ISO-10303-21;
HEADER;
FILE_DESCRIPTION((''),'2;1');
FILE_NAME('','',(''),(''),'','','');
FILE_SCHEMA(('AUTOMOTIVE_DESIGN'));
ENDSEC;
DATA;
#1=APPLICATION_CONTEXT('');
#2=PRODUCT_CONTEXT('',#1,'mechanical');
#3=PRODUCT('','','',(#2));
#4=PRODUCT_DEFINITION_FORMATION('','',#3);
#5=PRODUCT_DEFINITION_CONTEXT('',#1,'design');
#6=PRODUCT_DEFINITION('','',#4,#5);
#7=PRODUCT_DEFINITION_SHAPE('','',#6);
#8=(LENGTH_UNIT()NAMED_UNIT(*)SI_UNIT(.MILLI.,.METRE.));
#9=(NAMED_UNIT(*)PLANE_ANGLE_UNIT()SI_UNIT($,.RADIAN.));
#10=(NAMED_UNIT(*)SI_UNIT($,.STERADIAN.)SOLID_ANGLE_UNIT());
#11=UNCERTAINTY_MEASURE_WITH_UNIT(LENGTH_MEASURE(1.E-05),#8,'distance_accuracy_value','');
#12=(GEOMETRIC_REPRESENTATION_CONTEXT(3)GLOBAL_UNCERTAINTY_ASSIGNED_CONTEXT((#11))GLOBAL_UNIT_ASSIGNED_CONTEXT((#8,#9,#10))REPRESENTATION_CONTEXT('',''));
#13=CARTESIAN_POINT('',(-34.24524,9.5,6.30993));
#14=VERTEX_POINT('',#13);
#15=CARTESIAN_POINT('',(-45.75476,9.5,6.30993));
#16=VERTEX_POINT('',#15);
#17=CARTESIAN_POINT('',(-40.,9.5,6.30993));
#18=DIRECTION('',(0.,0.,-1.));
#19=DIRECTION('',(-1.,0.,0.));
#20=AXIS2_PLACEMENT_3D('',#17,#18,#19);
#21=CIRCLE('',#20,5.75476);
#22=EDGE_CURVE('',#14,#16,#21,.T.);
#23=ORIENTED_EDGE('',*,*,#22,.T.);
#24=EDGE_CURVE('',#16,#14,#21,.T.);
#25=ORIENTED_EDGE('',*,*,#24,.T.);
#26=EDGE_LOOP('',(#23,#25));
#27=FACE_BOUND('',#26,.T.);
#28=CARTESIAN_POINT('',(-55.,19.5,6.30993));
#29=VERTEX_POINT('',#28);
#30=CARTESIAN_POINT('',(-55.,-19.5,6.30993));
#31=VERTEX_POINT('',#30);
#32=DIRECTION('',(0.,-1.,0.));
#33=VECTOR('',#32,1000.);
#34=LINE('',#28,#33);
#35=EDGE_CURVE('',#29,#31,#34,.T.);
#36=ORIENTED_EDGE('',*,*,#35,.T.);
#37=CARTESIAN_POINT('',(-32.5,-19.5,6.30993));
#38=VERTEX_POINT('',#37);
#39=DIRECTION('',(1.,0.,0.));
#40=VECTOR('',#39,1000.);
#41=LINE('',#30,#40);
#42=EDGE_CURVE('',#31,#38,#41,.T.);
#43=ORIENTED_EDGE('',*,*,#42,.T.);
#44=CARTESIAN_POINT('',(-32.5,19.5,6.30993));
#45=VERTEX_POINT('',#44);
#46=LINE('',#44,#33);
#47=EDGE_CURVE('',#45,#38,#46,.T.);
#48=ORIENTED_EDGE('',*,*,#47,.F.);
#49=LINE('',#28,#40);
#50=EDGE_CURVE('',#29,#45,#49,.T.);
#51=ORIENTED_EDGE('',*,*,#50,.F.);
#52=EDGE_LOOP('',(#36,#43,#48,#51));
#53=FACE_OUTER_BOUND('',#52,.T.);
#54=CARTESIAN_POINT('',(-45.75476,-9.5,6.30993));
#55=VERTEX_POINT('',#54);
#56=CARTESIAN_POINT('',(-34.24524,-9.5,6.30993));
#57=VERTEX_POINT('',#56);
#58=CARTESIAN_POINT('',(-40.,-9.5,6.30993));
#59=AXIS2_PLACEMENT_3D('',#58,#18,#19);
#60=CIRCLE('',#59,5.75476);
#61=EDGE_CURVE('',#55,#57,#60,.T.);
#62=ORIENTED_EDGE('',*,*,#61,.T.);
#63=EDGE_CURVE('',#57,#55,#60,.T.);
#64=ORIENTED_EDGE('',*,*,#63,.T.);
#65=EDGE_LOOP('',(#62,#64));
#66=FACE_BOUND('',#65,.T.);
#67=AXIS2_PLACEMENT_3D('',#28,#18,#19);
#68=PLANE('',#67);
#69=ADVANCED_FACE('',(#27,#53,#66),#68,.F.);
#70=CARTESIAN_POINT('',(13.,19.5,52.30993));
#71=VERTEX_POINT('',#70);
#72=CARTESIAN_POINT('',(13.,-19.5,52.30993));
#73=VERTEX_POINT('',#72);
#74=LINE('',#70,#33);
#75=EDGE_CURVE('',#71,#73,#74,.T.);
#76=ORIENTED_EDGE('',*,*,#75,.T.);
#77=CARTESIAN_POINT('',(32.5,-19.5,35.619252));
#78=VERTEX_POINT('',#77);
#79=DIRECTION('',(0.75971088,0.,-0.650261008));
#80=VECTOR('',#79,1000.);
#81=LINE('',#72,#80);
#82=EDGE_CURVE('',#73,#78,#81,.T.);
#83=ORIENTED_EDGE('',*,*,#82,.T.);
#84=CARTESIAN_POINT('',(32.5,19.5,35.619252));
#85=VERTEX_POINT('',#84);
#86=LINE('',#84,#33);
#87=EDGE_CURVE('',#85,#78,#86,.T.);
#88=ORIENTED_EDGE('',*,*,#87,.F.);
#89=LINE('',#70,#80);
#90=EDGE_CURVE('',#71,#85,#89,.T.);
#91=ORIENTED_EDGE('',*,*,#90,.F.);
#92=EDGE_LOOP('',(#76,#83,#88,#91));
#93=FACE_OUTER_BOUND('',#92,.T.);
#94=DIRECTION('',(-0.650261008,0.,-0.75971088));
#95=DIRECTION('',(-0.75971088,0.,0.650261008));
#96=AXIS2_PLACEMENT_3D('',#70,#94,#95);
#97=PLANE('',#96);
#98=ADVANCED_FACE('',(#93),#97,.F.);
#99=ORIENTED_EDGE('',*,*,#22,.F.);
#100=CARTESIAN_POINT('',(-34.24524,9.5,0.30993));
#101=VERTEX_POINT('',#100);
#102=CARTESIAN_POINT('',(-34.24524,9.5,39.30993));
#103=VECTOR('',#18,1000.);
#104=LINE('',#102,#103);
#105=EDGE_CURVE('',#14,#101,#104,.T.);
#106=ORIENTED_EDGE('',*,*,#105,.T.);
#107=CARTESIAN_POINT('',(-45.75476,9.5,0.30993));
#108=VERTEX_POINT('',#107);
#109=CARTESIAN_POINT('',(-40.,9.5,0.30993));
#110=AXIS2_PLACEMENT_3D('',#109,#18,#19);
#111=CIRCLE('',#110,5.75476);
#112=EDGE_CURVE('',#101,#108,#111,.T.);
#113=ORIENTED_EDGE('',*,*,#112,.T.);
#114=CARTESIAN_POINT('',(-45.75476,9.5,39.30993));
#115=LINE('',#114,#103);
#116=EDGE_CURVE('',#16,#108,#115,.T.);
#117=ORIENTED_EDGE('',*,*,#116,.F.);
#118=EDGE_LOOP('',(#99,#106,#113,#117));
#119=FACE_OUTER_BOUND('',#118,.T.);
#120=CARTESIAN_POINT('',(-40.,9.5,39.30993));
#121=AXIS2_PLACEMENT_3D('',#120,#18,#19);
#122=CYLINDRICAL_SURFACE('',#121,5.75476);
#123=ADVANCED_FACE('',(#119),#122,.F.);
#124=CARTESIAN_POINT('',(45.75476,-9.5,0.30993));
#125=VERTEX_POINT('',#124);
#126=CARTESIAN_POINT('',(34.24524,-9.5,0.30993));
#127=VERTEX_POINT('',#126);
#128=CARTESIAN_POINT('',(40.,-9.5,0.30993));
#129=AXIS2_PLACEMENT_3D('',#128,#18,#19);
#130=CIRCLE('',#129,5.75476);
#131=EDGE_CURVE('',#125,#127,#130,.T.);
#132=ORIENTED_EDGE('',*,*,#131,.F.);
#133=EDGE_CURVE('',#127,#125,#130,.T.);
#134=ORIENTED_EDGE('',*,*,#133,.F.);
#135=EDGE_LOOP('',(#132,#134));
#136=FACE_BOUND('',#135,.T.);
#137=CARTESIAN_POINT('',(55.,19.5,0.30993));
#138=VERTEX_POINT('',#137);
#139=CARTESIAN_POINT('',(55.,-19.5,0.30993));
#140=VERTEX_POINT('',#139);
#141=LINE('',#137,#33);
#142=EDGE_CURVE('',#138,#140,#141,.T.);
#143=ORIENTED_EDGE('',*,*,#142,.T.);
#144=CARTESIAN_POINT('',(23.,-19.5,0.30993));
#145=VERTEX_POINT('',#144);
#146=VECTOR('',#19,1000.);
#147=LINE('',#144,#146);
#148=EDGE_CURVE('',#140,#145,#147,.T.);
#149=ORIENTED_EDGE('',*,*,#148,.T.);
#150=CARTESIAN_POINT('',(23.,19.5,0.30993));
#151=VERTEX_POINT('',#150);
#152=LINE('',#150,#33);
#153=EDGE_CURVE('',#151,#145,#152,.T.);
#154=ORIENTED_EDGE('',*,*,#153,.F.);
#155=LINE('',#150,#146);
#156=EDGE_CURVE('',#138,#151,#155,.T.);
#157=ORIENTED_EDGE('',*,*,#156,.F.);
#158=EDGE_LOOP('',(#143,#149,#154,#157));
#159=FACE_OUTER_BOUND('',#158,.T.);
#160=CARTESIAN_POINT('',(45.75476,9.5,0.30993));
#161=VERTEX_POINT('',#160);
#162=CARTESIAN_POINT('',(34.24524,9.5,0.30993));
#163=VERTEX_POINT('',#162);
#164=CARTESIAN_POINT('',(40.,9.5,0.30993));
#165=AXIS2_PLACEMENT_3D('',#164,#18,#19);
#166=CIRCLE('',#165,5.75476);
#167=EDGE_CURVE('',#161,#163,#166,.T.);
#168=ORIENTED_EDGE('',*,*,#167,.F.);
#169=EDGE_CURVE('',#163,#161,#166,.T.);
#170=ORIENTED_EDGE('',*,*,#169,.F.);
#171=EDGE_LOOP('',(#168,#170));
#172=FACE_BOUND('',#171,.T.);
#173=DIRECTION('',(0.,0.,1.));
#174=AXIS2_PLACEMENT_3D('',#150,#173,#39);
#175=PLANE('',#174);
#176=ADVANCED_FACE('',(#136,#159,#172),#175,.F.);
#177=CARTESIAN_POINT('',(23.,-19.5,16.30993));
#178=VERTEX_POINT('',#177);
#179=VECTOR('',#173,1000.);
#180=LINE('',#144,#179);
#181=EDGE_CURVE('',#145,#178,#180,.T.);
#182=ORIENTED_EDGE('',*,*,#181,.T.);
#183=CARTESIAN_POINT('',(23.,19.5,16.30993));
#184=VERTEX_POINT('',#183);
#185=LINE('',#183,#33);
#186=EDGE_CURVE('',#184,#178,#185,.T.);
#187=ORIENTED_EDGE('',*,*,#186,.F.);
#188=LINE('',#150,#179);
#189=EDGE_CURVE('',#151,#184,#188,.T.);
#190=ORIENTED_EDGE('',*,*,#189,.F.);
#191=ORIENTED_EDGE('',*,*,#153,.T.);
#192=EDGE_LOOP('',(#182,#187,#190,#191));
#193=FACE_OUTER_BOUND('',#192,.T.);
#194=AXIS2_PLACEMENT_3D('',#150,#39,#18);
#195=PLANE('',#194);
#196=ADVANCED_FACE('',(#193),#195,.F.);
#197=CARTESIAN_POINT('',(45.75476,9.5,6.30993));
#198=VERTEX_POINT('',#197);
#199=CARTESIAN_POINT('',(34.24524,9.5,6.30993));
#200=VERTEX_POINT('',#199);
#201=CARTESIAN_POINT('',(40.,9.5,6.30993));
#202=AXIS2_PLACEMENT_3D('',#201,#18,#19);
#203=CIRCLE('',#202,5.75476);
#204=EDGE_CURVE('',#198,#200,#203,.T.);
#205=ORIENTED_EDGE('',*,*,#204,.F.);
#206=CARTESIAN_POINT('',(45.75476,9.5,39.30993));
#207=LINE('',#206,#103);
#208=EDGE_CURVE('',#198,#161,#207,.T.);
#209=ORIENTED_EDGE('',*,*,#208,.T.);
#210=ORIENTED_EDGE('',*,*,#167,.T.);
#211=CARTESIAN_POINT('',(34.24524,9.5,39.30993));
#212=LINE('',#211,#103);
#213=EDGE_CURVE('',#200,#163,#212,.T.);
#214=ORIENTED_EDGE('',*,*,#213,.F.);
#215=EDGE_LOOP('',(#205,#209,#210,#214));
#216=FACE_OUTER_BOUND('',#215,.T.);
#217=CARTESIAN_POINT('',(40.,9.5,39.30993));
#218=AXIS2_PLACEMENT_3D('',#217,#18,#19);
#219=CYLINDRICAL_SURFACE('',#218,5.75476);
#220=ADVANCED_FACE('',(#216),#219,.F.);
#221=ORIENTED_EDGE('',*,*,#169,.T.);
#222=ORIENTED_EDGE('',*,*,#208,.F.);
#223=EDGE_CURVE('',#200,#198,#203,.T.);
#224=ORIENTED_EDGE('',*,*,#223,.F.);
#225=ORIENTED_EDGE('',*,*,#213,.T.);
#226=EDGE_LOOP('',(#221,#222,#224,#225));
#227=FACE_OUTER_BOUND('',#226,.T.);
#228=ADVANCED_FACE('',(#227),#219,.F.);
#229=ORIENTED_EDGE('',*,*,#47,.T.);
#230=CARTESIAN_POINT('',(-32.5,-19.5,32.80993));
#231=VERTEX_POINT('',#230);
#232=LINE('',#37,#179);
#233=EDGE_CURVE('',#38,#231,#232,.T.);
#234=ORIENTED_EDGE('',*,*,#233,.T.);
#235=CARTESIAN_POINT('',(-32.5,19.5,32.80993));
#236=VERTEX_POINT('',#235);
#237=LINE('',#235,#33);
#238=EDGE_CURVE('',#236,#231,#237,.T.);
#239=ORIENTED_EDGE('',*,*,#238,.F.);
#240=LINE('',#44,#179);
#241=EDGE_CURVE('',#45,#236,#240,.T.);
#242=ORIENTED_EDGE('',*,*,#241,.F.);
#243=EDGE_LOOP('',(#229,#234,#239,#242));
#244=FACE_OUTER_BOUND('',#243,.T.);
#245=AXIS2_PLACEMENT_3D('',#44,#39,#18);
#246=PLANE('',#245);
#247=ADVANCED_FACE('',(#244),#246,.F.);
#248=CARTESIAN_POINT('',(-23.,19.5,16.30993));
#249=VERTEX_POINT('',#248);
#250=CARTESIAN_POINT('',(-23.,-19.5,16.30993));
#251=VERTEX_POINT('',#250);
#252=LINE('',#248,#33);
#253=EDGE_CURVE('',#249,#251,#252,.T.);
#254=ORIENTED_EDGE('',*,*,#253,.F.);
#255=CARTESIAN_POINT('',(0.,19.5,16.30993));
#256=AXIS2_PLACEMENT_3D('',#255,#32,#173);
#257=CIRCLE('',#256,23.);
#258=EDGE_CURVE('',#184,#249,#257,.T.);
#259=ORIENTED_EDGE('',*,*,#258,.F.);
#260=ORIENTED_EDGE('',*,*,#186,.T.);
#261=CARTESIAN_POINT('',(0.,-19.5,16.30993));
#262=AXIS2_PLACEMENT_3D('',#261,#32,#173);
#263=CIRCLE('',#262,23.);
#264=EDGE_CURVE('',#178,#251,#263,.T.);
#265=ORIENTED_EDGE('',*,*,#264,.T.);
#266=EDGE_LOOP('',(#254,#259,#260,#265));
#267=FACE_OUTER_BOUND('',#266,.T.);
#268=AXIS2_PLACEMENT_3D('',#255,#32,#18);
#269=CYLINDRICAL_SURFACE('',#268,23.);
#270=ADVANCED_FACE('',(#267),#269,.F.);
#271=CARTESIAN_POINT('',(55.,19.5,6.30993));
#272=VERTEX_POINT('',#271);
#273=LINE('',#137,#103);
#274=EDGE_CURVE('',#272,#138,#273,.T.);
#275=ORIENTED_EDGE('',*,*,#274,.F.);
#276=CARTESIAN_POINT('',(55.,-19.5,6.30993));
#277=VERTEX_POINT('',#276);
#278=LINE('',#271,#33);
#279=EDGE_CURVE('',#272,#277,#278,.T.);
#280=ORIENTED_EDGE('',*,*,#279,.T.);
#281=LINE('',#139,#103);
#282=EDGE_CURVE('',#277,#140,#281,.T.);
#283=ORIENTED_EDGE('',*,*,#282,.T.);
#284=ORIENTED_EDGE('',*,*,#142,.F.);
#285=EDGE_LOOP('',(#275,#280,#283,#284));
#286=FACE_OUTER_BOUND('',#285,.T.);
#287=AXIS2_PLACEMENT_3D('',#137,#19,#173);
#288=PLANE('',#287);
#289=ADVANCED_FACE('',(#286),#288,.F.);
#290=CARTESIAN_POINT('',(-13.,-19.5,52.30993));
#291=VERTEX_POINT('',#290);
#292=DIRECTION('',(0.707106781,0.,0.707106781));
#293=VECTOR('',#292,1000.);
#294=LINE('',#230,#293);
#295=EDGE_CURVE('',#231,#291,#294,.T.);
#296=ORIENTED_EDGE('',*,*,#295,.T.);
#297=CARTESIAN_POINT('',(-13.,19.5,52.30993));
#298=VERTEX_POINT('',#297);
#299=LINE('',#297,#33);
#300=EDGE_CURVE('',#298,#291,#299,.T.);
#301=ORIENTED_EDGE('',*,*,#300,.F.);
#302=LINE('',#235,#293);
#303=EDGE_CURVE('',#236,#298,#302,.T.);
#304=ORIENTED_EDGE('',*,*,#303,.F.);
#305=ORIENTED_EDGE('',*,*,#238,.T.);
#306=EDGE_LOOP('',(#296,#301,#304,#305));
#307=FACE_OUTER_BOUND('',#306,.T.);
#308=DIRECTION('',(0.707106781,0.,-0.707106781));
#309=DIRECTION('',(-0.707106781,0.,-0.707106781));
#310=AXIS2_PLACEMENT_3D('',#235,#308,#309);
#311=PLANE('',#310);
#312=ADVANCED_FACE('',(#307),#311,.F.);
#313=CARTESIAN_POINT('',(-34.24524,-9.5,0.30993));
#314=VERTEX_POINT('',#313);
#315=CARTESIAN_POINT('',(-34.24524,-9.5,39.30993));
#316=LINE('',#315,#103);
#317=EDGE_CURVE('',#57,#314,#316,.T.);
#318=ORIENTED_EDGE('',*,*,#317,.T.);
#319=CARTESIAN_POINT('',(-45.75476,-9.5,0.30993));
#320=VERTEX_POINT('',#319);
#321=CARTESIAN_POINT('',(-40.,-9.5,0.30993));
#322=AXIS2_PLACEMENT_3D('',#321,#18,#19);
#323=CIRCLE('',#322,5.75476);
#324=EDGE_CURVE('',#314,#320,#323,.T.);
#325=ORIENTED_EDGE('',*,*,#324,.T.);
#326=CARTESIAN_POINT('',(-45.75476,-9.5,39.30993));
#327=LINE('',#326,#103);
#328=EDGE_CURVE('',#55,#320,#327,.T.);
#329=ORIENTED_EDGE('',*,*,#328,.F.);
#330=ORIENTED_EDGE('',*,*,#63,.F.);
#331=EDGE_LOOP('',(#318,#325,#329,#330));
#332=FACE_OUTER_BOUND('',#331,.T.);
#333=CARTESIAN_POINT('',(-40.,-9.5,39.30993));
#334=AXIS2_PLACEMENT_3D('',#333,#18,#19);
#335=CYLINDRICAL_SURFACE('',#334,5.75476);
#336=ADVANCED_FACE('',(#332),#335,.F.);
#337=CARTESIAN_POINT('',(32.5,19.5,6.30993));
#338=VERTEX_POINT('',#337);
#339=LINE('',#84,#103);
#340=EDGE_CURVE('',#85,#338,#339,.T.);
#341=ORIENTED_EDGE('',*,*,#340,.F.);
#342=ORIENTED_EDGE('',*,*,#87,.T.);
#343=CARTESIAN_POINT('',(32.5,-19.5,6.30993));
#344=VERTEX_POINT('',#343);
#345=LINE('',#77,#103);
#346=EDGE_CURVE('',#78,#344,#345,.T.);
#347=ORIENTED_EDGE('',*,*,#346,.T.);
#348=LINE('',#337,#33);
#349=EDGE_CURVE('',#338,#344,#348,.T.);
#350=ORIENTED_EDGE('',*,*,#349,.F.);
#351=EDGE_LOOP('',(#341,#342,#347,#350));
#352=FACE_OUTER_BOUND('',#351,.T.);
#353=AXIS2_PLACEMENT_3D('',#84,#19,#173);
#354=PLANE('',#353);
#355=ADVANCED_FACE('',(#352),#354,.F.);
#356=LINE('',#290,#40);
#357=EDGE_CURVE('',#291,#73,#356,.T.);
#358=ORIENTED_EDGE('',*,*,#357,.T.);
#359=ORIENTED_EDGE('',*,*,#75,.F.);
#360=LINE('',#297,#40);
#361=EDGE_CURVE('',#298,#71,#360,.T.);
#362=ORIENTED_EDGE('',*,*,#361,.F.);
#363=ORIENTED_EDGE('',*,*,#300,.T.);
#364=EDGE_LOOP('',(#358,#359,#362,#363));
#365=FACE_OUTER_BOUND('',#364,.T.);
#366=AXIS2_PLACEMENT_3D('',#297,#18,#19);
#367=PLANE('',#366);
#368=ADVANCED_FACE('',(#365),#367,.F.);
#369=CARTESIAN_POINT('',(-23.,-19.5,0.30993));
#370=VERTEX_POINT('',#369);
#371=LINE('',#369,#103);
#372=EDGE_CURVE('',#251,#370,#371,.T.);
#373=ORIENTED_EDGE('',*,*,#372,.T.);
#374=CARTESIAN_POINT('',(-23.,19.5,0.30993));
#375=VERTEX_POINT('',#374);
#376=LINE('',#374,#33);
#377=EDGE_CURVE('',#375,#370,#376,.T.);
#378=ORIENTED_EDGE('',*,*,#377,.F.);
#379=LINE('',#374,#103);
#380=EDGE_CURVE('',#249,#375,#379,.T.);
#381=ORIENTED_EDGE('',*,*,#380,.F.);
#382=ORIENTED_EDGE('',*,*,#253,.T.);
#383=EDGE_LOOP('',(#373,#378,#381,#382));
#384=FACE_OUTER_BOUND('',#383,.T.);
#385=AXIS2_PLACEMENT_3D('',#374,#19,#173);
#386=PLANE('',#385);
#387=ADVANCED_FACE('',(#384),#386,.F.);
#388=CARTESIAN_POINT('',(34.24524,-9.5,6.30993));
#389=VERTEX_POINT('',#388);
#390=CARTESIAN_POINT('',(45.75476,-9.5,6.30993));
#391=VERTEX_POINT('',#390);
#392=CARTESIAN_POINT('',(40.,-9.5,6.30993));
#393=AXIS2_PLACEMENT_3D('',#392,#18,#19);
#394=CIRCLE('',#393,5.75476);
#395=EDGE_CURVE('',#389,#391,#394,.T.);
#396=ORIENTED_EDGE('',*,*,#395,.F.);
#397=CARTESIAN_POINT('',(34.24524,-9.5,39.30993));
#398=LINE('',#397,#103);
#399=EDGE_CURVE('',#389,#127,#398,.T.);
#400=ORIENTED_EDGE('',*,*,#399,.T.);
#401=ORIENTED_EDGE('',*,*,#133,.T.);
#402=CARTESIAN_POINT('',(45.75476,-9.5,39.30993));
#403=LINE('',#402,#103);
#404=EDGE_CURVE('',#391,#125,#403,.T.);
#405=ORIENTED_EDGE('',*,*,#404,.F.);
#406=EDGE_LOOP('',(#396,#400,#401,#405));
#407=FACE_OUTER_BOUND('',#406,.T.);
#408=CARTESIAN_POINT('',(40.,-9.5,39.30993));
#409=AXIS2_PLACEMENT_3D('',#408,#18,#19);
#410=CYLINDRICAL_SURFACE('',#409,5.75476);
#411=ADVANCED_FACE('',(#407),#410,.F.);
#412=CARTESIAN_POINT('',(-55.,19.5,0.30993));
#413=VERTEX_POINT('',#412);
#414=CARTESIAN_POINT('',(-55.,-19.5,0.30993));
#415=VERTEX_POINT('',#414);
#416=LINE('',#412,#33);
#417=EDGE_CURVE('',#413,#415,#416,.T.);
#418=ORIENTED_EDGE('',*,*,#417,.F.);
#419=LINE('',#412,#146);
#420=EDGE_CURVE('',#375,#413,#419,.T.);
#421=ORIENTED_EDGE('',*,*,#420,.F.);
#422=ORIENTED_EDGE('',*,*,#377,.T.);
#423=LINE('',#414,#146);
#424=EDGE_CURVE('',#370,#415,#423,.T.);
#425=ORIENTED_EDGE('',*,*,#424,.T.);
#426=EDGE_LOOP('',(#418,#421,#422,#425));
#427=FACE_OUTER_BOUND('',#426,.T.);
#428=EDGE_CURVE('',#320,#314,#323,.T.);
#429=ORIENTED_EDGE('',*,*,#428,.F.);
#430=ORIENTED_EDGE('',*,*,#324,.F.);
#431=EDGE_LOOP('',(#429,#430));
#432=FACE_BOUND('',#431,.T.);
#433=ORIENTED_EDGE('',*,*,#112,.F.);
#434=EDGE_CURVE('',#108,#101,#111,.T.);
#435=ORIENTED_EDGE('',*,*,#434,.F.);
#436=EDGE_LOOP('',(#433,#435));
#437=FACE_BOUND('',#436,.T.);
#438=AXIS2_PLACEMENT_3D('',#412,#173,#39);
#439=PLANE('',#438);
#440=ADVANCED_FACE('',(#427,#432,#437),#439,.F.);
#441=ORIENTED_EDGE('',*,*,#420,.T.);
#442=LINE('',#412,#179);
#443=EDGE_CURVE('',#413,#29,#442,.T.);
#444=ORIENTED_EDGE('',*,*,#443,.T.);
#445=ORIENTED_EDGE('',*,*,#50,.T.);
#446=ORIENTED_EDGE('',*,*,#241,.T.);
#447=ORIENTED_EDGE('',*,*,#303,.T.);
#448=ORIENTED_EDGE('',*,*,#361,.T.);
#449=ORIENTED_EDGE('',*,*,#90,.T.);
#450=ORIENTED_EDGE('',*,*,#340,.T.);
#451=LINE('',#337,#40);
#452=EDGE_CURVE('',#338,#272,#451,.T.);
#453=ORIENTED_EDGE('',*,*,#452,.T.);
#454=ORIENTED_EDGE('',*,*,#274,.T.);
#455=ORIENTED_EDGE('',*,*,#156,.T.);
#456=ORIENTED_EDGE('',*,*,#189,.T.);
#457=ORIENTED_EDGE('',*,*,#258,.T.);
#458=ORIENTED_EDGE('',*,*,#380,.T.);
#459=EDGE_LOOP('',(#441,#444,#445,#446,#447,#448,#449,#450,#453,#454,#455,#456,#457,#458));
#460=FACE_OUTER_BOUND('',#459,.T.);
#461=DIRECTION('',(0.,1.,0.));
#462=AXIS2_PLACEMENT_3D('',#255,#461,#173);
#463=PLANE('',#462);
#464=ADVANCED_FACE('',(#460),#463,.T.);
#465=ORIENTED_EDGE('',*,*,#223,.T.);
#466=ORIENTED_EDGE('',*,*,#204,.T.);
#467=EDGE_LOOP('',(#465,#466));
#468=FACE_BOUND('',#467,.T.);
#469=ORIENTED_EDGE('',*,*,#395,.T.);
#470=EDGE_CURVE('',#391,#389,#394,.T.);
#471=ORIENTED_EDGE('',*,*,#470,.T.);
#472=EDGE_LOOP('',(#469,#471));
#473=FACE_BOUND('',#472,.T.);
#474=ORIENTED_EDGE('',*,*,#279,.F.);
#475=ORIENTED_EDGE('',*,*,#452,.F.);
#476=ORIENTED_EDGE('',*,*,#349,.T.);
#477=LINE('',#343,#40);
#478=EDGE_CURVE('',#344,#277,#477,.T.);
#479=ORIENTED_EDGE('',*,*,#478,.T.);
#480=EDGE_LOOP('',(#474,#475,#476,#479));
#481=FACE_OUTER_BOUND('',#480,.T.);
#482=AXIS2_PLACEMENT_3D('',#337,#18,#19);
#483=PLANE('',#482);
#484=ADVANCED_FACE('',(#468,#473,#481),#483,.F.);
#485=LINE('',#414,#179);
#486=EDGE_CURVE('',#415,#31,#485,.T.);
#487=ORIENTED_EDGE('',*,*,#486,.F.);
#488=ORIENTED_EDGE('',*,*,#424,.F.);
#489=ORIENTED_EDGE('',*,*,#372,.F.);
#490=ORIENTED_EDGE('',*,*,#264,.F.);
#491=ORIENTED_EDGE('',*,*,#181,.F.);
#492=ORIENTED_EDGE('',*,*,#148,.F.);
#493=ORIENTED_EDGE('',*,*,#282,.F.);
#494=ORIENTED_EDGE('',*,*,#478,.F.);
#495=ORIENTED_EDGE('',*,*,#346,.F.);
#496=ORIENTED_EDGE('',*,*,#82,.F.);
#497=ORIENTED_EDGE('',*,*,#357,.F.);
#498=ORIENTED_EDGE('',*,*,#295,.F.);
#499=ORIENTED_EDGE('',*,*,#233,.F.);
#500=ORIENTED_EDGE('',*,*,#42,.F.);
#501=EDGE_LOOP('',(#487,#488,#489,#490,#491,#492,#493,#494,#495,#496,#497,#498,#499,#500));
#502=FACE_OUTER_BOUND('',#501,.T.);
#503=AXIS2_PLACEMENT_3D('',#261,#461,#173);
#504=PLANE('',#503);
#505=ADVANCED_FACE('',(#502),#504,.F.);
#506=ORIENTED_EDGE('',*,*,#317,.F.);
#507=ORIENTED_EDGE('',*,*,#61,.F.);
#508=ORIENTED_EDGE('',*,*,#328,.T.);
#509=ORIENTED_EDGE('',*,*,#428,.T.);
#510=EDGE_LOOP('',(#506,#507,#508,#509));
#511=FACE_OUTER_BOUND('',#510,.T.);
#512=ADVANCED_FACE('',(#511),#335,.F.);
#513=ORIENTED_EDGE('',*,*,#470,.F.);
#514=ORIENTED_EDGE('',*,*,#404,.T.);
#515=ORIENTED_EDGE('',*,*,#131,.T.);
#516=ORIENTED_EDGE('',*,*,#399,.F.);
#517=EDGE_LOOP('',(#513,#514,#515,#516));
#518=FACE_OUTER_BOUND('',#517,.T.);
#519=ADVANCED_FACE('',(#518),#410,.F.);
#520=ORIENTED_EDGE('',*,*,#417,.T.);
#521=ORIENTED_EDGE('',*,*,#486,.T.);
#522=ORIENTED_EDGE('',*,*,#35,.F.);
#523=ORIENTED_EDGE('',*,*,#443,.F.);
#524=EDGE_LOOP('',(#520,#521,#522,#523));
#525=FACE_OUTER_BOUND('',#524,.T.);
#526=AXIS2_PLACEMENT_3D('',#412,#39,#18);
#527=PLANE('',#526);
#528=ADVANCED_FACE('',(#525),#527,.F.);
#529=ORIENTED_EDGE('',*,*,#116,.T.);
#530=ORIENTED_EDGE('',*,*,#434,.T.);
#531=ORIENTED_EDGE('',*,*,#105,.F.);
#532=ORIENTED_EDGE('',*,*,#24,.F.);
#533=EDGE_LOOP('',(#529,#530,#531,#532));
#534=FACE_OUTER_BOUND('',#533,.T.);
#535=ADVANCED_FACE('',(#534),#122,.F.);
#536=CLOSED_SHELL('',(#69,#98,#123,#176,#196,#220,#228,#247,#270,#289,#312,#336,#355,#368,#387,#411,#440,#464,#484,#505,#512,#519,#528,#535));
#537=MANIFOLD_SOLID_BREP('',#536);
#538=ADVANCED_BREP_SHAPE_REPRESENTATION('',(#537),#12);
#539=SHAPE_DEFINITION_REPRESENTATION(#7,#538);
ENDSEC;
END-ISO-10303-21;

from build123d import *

# Parameters (mm, degrees)
SADDLE_BODY_DEPTH       = 19.5
FLANGE_HOLES_SKETCH_R   = 5.754759715
FLANGE_BOLT_HOLES_DEPTH = 39


with BuildPart() as part:
    # Saddle Profile Sketch → Saddle Body (new, symmetric)
    with BuildSketch(Plane(origin=(0, 0, 0), x_dir=(1, 0, 0), z_dir=(0, 1, 0))):
        with BuildLine():
            Line((-23, -0.309929889), (-23, -16.309929889))
            ThreePointArc((-23, -16.309929889), (0, -39.309929889), (23, -16.309929889))
            Line((23, -16.309929889), (23, -0.309929889))
            Line((23, -0.309929889), (55, -0.309929889))
            Line((55, -0.309929889), (55, -6.309929889))
            Line((55, -6.309929889), (32.5, -6.309929889))
            Line((32.5, -6.309929889), (32.5, -35.619251923))
            Line((32.5, -35.619251923), (13, -52.309929889))
            Line((13, -52.309929889), (-13, -52.309929889))
            Line((-13, -52.309929889), (-32.5, -32.809929889))
            Line((-32.5, -32.809929889), (-32.5, -6.309929889))
            Line((-32.5, -6.309929889), (-55, -6.309929889))
            Line((-55, -6.309929889), (-55, -0.309929889))
            Line((-55, -0.309929889), (-23, -0.309929889))
        make_face()
    extrude(amount=SADDLE_BODY_DEPTH, both=True)

    # Flange Holes Sketch → Flange Bolt Holes (cut)
    with BuildSketch(Plane(origin=(0, 0, 0.309929889), x_dir=(-1, 0, 0), z_dir=(0, 0, -1))):
        with Locations((-40, 9.5)):
            Circle(FLANGE_HOLES_SKETCH_R)
        with Locations((40, 9.5)):
            Circle(FLANGE_HOLES_SKETCH_R)
        with Locations((40, -9.5)):
            Circle(FLANGE_HOLES_SKETCH_R)
        with Locations((-40, -9.5)):
            Circle(FLANGE_HOLES_SKETCH_R)
    extrude(amount=-FLANGE_BOLT_HOLES_DEPTH, mode=Mode.SUBTRACT)


solid = part.part
